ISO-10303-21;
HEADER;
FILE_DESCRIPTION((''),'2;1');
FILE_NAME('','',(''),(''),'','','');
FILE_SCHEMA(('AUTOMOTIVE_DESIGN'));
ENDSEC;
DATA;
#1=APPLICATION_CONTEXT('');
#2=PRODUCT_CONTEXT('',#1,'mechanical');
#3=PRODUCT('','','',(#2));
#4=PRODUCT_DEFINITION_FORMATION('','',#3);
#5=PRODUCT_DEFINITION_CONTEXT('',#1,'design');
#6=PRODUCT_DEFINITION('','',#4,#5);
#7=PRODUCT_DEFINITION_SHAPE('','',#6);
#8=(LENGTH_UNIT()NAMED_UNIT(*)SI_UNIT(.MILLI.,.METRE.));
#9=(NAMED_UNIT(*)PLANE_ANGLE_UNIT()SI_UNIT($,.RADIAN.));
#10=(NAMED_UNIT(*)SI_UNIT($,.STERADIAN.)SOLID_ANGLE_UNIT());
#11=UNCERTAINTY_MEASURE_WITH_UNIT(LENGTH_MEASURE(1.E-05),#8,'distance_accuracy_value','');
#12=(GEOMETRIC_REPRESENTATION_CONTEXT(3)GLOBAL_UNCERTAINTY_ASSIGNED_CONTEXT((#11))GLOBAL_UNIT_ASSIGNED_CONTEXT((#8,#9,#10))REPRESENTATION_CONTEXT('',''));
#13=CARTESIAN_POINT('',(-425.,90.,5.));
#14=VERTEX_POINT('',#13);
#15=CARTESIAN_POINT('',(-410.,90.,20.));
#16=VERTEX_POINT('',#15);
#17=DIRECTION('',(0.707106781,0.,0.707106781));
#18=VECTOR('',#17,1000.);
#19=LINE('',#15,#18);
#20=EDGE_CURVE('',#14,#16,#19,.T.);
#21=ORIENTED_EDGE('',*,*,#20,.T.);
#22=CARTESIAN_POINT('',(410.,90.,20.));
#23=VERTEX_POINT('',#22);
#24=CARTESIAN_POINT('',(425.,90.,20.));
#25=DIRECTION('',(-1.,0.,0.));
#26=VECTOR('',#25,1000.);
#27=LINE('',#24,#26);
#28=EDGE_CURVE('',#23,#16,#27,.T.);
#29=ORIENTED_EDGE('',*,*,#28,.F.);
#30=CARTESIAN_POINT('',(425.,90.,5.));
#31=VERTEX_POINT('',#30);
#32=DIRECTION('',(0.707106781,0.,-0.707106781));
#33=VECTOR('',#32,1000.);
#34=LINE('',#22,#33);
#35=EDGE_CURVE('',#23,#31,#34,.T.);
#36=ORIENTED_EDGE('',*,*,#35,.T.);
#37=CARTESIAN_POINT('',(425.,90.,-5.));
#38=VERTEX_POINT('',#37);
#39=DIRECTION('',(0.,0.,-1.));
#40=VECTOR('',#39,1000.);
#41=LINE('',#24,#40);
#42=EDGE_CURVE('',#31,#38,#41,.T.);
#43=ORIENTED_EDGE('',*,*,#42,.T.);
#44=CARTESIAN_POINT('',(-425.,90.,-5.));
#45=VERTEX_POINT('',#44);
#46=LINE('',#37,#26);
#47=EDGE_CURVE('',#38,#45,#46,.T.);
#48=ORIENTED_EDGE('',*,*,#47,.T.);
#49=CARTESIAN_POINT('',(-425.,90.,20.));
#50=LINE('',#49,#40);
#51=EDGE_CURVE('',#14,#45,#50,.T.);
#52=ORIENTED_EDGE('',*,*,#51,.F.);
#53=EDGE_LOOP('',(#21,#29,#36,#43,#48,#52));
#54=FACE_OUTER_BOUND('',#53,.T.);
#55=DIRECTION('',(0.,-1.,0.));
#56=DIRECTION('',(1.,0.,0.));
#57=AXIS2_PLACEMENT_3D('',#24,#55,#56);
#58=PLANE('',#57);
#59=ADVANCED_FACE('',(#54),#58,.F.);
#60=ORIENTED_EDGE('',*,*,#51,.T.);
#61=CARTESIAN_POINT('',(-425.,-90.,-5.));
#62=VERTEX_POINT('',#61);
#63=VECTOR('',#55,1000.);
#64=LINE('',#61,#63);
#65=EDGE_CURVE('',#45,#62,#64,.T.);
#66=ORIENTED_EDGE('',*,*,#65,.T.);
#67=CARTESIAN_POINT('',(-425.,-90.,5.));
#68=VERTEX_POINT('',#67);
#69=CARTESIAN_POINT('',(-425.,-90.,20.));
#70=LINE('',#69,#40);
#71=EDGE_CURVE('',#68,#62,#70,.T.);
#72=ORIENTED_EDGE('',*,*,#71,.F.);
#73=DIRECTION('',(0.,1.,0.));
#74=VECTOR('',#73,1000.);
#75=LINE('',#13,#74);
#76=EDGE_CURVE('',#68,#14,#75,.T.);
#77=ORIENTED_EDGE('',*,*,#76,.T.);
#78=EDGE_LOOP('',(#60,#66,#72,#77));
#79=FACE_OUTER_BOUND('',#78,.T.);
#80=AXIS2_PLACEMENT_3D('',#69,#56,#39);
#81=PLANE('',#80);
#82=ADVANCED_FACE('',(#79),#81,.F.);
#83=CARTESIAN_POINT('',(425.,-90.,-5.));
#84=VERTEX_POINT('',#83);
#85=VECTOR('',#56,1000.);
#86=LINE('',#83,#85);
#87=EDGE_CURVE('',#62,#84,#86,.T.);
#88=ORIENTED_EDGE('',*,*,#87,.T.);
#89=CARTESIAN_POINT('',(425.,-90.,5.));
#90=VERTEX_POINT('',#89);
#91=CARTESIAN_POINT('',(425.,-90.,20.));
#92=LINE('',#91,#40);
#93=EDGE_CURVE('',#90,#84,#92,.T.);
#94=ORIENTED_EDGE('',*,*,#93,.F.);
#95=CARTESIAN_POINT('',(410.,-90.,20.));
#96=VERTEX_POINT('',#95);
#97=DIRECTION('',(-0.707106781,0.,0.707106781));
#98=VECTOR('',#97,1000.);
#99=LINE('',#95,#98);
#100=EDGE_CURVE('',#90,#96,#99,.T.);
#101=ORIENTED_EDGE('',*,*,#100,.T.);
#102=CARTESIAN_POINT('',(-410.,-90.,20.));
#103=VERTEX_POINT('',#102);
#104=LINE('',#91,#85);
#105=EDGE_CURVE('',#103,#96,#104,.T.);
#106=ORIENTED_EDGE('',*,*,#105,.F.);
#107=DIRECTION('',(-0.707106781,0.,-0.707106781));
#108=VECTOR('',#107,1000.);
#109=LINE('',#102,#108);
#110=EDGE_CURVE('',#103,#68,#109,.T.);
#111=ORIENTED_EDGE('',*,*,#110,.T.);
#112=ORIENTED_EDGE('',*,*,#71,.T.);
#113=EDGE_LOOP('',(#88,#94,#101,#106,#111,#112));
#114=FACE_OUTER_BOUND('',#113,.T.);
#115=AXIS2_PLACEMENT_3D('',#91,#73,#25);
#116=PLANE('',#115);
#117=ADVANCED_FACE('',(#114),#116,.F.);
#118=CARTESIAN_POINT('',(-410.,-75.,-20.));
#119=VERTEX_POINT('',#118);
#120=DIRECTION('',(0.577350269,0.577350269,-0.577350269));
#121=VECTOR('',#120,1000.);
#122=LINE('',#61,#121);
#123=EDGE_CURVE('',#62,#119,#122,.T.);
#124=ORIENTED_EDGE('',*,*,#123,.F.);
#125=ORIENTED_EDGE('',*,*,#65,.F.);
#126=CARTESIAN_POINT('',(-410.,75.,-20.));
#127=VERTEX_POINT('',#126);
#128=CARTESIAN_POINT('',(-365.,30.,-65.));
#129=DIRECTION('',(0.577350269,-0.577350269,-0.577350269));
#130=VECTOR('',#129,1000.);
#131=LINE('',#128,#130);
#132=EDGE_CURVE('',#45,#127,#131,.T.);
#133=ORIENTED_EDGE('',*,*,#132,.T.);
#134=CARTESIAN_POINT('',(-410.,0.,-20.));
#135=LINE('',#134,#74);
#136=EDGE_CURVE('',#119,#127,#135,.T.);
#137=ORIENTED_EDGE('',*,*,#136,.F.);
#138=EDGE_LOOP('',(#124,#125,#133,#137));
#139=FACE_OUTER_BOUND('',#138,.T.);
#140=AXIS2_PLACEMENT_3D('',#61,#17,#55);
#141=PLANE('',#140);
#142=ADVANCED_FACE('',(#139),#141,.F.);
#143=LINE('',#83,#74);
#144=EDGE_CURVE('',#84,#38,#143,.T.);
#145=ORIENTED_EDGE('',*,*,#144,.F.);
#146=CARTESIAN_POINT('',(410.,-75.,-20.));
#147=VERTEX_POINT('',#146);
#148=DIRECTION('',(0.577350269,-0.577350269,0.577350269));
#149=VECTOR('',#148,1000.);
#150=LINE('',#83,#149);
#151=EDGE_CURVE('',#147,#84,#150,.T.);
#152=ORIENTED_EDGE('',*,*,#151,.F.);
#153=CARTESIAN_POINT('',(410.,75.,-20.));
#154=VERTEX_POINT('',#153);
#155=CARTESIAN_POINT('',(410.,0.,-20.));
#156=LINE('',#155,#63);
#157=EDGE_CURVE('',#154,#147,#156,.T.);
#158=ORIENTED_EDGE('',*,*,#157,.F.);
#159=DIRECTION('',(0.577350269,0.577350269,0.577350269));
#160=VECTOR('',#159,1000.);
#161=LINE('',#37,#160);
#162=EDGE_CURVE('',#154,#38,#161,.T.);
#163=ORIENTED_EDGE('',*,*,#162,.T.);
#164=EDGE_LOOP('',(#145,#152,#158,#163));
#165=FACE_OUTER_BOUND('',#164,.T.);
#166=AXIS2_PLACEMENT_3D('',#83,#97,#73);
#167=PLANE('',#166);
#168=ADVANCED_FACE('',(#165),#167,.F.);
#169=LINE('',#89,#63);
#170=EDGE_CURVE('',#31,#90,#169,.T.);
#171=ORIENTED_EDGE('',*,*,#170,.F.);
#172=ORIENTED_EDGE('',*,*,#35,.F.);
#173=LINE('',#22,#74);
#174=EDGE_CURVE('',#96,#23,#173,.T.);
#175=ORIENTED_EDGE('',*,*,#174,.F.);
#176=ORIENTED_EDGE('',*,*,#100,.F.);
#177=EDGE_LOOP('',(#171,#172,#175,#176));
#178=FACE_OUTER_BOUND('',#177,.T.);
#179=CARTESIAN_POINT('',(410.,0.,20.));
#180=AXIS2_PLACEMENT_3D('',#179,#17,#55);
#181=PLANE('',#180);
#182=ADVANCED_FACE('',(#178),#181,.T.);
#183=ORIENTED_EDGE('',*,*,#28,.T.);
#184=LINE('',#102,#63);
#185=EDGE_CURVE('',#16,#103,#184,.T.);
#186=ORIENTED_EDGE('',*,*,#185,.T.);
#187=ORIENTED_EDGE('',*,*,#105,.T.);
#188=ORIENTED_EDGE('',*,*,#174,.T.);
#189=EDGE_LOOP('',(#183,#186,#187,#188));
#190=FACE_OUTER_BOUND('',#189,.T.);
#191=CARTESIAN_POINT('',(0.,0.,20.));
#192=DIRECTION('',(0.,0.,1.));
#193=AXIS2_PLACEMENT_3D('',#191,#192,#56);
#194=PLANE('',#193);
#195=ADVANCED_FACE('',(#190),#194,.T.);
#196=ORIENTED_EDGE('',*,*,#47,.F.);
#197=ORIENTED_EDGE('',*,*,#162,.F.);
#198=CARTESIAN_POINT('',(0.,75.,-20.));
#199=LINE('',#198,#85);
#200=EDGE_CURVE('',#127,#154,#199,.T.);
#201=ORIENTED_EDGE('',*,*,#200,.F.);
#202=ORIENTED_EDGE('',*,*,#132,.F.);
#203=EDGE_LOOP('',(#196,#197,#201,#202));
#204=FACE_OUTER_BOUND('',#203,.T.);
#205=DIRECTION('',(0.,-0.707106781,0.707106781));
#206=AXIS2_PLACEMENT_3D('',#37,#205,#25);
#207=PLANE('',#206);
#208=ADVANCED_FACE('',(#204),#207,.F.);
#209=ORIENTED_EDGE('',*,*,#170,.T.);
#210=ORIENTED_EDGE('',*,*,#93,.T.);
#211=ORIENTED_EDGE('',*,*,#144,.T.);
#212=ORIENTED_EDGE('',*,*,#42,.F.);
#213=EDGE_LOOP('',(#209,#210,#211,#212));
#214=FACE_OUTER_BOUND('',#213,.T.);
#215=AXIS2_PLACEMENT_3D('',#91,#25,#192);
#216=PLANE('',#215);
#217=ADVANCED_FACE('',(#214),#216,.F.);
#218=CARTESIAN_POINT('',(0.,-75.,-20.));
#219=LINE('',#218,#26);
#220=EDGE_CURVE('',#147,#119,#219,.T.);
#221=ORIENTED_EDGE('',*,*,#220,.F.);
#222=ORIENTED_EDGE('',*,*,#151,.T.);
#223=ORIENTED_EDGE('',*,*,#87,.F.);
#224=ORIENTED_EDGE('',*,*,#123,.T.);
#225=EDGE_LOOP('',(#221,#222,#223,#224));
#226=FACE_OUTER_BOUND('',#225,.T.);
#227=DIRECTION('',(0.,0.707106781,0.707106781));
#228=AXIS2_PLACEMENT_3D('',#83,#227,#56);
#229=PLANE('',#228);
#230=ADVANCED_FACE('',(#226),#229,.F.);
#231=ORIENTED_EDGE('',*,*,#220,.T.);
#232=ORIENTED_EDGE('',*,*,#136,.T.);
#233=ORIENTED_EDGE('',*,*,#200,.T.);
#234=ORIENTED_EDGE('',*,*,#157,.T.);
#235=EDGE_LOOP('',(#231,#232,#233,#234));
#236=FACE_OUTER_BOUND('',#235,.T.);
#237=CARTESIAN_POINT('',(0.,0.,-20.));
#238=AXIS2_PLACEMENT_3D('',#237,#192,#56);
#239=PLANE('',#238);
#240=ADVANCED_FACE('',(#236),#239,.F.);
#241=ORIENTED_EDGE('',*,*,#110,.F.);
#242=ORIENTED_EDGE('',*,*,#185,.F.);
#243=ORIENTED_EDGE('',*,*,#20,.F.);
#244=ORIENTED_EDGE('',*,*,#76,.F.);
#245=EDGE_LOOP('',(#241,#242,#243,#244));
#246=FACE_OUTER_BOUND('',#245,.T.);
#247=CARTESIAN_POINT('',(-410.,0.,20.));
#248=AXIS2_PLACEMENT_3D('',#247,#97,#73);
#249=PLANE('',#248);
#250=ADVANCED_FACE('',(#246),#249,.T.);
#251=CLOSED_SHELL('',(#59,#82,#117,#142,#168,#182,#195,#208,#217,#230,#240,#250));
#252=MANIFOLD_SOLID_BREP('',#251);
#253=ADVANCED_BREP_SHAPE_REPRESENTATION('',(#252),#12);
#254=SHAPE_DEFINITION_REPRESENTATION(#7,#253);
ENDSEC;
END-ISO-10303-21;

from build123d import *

# Parameters (mm, degrees)
SKETCH1_W           = 850
SKETCH1_H           = 180
BOSS_EXTRUDE1_DEPTH = 20
CHAMFER1_SIZE       = 15


with BuildPart() as part:
    # Sketch1 → Boss-Extrude1 (new, symmetric)
    with BuildSketch(Plane.XY):
        Rectangle(SKETCH1_W, SKETCH1_H)
    extrude(amount=BOSS_EXTRUDE1_DEPTH, both=True)

    # Chamfer1
    chamfer1_edges = [part.edges().sort_by_distance(p)[0] for p in [
        (425, 0, 20),
        (-425, 0, 20),
        (0, 90, -20),
        (425, 0, -20),
        (0, -90, -20),
        (-425, 0, -20),
    ]]
    chamfer(chamfer1_edges, length=CHAMFER1_SIZE)


solid = part.part
